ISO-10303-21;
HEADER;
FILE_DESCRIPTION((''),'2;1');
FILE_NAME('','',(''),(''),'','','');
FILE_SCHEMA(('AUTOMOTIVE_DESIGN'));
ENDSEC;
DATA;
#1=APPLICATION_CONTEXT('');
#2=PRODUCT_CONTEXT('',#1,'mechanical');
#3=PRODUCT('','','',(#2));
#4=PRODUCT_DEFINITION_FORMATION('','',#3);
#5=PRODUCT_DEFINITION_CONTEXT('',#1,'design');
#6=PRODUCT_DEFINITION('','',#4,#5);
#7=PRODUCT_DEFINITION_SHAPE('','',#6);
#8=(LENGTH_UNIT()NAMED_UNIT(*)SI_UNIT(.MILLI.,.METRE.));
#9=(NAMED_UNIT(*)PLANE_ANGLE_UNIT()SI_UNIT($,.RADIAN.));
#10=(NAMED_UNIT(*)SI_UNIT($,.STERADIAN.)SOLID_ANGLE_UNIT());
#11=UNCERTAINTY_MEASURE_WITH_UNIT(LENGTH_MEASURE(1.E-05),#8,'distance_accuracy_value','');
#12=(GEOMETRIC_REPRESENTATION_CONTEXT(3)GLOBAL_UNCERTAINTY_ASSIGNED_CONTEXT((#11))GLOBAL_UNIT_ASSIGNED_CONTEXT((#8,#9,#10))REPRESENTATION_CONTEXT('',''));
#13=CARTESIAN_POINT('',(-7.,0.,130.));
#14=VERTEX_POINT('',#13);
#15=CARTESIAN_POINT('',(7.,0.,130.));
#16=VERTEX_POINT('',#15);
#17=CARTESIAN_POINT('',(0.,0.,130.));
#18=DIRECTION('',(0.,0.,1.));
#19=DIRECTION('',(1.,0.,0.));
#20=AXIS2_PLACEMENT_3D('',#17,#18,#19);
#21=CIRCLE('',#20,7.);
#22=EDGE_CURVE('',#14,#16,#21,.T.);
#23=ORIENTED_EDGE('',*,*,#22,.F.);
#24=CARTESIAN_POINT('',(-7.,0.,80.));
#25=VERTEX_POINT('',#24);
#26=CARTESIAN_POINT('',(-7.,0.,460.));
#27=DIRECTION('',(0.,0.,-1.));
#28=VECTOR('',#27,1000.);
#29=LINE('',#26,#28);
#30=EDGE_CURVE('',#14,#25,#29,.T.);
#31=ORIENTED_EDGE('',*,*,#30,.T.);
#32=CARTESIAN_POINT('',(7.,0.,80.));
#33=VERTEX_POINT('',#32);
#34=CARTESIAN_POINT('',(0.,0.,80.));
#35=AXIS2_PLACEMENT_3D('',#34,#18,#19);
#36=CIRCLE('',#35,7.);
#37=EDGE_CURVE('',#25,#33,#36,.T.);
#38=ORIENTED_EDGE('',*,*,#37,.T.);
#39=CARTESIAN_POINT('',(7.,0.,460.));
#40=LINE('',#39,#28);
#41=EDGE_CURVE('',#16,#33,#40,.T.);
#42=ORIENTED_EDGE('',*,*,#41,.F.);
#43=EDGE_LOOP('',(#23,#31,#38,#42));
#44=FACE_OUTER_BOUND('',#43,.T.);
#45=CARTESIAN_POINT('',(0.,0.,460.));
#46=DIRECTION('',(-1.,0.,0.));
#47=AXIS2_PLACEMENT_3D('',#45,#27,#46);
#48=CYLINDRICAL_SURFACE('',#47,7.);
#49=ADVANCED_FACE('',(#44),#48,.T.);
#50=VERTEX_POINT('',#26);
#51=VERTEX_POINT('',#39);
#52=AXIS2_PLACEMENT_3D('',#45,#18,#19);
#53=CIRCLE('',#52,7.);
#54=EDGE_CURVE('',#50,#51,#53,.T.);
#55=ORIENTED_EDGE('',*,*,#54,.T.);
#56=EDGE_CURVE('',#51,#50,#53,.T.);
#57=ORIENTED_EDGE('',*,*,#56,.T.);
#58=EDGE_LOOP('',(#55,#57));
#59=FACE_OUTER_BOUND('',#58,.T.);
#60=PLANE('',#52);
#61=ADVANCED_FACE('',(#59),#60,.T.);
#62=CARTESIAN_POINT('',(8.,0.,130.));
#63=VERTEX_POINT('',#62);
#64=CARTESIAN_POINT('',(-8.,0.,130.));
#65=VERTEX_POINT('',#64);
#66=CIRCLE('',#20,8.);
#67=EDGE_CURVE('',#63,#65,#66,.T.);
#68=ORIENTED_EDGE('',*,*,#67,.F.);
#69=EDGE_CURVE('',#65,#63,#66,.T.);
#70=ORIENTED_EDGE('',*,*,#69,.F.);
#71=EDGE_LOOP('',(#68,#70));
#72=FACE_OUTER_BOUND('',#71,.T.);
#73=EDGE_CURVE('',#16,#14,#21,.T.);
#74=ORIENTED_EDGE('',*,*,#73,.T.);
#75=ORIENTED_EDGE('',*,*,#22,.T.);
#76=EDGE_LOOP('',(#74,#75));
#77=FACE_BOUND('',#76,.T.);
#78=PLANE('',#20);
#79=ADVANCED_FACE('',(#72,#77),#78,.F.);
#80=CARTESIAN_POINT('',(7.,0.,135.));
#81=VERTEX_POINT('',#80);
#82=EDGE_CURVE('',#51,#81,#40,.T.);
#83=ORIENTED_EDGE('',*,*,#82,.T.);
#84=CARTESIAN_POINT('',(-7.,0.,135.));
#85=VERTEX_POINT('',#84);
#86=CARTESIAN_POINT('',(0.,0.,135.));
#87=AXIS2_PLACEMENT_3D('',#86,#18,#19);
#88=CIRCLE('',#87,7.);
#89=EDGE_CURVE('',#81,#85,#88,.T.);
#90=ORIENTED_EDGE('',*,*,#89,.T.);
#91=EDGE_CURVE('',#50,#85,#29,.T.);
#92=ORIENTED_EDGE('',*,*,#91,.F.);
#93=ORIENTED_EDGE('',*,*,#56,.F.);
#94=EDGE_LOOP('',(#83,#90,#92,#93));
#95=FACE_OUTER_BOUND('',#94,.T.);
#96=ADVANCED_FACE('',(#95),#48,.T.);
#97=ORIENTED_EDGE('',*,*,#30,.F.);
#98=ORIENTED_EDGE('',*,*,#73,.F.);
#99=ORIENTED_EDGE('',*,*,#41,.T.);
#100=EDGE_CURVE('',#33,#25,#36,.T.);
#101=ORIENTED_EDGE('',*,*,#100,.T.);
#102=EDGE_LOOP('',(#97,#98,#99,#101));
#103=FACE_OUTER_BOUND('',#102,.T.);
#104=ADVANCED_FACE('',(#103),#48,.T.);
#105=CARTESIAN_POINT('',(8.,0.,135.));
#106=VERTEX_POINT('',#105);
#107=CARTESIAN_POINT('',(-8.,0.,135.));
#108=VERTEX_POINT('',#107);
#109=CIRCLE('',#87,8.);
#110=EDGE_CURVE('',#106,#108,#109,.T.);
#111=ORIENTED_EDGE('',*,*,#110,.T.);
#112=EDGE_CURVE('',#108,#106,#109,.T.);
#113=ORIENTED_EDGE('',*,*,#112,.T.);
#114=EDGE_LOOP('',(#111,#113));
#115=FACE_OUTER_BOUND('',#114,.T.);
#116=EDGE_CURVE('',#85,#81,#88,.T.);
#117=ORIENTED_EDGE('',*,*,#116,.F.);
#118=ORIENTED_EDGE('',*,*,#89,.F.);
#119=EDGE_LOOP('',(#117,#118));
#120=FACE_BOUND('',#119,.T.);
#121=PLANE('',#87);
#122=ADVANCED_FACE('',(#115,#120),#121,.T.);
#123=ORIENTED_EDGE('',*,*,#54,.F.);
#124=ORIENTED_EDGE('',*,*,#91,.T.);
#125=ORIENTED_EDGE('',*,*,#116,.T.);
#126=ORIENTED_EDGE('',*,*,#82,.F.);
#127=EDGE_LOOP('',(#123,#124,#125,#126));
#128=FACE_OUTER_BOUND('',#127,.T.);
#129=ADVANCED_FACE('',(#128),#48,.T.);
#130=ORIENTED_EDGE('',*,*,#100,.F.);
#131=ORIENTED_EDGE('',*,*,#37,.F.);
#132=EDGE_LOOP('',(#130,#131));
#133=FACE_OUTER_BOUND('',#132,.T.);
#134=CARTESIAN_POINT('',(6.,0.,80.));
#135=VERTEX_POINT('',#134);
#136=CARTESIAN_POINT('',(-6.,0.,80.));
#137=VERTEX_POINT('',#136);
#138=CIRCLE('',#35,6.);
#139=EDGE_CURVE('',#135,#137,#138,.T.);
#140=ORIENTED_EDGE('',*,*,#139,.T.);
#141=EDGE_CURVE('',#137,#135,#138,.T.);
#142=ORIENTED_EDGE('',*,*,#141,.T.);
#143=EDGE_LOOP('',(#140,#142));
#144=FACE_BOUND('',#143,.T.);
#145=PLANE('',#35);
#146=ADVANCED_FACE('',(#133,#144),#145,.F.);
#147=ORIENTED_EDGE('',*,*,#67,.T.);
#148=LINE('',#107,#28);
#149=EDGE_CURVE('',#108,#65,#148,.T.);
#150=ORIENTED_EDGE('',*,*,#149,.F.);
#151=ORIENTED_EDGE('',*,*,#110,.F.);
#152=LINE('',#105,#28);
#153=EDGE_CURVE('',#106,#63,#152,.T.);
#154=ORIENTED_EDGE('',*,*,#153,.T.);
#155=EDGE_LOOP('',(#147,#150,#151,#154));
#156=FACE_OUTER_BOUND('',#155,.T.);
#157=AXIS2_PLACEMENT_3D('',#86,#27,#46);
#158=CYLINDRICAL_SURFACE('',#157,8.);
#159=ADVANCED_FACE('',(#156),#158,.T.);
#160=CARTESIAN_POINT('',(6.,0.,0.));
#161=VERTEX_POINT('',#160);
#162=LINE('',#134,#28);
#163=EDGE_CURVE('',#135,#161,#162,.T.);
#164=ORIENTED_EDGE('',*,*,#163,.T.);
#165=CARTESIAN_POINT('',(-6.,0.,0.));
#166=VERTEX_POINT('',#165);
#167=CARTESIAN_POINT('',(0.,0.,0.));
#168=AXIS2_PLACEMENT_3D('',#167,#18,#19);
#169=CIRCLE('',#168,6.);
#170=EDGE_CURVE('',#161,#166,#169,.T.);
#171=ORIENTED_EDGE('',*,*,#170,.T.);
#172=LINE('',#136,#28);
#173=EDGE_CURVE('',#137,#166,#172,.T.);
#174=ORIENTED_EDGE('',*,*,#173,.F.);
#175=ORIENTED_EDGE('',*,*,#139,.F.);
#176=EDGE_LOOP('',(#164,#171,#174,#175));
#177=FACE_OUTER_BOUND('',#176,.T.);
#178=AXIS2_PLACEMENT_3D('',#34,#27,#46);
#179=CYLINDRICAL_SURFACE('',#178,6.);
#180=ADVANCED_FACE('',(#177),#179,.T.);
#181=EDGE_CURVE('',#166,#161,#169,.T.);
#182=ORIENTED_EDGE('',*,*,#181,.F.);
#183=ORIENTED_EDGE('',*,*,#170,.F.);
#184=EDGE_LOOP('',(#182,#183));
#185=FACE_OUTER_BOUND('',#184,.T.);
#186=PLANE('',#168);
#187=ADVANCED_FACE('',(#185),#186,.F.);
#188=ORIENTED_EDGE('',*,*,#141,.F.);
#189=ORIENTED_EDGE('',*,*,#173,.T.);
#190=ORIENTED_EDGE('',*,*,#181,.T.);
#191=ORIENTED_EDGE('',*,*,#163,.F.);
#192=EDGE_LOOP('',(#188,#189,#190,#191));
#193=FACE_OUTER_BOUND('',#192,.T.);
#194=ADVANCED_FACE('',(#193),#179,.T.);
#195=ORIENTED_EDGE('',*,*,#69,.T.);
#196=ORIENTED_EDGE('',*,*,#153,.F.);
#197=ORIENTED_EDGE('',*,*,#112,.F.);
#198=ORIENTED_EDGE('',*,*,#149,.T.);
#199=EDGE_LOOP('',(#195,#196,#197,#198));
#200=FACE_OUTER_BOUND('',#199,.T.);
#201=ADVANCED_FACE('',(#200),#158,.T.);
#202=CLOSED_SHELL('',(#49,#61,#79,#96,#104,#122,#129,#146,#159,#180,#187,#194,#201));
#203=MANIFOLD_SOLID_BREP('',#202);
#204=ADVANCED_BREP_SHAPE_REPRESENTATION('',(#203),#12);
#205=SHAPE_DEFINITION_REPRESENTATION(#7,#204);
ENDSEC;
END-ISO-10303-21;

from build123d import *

# Parameters (mm, degrees)
SKETCH_1_R      = 6
EXTRUDE_1_DEPTH = 80
SKETCH_3_R      = 7
EXTRUDE_2_DEPTH = 380
EXTRUDE_START   = -330
SKETCH_4_R      = 8
EXTRUDE_3_DEPTH = 5


with BuildPart() as part:
    # 草图1 → 凸台-拉伸1 (new body)
    with BuildSketch(Plane.XY):
        Circle(SKETCH_1_R)
    extrude(amount=EXTRUDE_1_DEPTH)

    # 草图3 → 凸台-拉伸2 (add)
    with BuildSketch(Plane.XY.offset(80)):
        Circle(SKETCH_3_R)
    extrude(amount=EXTRUDE_2_DEPTH)

    # 草图4 → 凸台-拉伸3 (add)
    with BuildSketch(Plane.XY.offset(460).offset(EXTRUDE_START)):
        Circle(SKETCH_4_R)
    extrude(amount=EXTRUDE_3_DEPTH)


solid = part.part
